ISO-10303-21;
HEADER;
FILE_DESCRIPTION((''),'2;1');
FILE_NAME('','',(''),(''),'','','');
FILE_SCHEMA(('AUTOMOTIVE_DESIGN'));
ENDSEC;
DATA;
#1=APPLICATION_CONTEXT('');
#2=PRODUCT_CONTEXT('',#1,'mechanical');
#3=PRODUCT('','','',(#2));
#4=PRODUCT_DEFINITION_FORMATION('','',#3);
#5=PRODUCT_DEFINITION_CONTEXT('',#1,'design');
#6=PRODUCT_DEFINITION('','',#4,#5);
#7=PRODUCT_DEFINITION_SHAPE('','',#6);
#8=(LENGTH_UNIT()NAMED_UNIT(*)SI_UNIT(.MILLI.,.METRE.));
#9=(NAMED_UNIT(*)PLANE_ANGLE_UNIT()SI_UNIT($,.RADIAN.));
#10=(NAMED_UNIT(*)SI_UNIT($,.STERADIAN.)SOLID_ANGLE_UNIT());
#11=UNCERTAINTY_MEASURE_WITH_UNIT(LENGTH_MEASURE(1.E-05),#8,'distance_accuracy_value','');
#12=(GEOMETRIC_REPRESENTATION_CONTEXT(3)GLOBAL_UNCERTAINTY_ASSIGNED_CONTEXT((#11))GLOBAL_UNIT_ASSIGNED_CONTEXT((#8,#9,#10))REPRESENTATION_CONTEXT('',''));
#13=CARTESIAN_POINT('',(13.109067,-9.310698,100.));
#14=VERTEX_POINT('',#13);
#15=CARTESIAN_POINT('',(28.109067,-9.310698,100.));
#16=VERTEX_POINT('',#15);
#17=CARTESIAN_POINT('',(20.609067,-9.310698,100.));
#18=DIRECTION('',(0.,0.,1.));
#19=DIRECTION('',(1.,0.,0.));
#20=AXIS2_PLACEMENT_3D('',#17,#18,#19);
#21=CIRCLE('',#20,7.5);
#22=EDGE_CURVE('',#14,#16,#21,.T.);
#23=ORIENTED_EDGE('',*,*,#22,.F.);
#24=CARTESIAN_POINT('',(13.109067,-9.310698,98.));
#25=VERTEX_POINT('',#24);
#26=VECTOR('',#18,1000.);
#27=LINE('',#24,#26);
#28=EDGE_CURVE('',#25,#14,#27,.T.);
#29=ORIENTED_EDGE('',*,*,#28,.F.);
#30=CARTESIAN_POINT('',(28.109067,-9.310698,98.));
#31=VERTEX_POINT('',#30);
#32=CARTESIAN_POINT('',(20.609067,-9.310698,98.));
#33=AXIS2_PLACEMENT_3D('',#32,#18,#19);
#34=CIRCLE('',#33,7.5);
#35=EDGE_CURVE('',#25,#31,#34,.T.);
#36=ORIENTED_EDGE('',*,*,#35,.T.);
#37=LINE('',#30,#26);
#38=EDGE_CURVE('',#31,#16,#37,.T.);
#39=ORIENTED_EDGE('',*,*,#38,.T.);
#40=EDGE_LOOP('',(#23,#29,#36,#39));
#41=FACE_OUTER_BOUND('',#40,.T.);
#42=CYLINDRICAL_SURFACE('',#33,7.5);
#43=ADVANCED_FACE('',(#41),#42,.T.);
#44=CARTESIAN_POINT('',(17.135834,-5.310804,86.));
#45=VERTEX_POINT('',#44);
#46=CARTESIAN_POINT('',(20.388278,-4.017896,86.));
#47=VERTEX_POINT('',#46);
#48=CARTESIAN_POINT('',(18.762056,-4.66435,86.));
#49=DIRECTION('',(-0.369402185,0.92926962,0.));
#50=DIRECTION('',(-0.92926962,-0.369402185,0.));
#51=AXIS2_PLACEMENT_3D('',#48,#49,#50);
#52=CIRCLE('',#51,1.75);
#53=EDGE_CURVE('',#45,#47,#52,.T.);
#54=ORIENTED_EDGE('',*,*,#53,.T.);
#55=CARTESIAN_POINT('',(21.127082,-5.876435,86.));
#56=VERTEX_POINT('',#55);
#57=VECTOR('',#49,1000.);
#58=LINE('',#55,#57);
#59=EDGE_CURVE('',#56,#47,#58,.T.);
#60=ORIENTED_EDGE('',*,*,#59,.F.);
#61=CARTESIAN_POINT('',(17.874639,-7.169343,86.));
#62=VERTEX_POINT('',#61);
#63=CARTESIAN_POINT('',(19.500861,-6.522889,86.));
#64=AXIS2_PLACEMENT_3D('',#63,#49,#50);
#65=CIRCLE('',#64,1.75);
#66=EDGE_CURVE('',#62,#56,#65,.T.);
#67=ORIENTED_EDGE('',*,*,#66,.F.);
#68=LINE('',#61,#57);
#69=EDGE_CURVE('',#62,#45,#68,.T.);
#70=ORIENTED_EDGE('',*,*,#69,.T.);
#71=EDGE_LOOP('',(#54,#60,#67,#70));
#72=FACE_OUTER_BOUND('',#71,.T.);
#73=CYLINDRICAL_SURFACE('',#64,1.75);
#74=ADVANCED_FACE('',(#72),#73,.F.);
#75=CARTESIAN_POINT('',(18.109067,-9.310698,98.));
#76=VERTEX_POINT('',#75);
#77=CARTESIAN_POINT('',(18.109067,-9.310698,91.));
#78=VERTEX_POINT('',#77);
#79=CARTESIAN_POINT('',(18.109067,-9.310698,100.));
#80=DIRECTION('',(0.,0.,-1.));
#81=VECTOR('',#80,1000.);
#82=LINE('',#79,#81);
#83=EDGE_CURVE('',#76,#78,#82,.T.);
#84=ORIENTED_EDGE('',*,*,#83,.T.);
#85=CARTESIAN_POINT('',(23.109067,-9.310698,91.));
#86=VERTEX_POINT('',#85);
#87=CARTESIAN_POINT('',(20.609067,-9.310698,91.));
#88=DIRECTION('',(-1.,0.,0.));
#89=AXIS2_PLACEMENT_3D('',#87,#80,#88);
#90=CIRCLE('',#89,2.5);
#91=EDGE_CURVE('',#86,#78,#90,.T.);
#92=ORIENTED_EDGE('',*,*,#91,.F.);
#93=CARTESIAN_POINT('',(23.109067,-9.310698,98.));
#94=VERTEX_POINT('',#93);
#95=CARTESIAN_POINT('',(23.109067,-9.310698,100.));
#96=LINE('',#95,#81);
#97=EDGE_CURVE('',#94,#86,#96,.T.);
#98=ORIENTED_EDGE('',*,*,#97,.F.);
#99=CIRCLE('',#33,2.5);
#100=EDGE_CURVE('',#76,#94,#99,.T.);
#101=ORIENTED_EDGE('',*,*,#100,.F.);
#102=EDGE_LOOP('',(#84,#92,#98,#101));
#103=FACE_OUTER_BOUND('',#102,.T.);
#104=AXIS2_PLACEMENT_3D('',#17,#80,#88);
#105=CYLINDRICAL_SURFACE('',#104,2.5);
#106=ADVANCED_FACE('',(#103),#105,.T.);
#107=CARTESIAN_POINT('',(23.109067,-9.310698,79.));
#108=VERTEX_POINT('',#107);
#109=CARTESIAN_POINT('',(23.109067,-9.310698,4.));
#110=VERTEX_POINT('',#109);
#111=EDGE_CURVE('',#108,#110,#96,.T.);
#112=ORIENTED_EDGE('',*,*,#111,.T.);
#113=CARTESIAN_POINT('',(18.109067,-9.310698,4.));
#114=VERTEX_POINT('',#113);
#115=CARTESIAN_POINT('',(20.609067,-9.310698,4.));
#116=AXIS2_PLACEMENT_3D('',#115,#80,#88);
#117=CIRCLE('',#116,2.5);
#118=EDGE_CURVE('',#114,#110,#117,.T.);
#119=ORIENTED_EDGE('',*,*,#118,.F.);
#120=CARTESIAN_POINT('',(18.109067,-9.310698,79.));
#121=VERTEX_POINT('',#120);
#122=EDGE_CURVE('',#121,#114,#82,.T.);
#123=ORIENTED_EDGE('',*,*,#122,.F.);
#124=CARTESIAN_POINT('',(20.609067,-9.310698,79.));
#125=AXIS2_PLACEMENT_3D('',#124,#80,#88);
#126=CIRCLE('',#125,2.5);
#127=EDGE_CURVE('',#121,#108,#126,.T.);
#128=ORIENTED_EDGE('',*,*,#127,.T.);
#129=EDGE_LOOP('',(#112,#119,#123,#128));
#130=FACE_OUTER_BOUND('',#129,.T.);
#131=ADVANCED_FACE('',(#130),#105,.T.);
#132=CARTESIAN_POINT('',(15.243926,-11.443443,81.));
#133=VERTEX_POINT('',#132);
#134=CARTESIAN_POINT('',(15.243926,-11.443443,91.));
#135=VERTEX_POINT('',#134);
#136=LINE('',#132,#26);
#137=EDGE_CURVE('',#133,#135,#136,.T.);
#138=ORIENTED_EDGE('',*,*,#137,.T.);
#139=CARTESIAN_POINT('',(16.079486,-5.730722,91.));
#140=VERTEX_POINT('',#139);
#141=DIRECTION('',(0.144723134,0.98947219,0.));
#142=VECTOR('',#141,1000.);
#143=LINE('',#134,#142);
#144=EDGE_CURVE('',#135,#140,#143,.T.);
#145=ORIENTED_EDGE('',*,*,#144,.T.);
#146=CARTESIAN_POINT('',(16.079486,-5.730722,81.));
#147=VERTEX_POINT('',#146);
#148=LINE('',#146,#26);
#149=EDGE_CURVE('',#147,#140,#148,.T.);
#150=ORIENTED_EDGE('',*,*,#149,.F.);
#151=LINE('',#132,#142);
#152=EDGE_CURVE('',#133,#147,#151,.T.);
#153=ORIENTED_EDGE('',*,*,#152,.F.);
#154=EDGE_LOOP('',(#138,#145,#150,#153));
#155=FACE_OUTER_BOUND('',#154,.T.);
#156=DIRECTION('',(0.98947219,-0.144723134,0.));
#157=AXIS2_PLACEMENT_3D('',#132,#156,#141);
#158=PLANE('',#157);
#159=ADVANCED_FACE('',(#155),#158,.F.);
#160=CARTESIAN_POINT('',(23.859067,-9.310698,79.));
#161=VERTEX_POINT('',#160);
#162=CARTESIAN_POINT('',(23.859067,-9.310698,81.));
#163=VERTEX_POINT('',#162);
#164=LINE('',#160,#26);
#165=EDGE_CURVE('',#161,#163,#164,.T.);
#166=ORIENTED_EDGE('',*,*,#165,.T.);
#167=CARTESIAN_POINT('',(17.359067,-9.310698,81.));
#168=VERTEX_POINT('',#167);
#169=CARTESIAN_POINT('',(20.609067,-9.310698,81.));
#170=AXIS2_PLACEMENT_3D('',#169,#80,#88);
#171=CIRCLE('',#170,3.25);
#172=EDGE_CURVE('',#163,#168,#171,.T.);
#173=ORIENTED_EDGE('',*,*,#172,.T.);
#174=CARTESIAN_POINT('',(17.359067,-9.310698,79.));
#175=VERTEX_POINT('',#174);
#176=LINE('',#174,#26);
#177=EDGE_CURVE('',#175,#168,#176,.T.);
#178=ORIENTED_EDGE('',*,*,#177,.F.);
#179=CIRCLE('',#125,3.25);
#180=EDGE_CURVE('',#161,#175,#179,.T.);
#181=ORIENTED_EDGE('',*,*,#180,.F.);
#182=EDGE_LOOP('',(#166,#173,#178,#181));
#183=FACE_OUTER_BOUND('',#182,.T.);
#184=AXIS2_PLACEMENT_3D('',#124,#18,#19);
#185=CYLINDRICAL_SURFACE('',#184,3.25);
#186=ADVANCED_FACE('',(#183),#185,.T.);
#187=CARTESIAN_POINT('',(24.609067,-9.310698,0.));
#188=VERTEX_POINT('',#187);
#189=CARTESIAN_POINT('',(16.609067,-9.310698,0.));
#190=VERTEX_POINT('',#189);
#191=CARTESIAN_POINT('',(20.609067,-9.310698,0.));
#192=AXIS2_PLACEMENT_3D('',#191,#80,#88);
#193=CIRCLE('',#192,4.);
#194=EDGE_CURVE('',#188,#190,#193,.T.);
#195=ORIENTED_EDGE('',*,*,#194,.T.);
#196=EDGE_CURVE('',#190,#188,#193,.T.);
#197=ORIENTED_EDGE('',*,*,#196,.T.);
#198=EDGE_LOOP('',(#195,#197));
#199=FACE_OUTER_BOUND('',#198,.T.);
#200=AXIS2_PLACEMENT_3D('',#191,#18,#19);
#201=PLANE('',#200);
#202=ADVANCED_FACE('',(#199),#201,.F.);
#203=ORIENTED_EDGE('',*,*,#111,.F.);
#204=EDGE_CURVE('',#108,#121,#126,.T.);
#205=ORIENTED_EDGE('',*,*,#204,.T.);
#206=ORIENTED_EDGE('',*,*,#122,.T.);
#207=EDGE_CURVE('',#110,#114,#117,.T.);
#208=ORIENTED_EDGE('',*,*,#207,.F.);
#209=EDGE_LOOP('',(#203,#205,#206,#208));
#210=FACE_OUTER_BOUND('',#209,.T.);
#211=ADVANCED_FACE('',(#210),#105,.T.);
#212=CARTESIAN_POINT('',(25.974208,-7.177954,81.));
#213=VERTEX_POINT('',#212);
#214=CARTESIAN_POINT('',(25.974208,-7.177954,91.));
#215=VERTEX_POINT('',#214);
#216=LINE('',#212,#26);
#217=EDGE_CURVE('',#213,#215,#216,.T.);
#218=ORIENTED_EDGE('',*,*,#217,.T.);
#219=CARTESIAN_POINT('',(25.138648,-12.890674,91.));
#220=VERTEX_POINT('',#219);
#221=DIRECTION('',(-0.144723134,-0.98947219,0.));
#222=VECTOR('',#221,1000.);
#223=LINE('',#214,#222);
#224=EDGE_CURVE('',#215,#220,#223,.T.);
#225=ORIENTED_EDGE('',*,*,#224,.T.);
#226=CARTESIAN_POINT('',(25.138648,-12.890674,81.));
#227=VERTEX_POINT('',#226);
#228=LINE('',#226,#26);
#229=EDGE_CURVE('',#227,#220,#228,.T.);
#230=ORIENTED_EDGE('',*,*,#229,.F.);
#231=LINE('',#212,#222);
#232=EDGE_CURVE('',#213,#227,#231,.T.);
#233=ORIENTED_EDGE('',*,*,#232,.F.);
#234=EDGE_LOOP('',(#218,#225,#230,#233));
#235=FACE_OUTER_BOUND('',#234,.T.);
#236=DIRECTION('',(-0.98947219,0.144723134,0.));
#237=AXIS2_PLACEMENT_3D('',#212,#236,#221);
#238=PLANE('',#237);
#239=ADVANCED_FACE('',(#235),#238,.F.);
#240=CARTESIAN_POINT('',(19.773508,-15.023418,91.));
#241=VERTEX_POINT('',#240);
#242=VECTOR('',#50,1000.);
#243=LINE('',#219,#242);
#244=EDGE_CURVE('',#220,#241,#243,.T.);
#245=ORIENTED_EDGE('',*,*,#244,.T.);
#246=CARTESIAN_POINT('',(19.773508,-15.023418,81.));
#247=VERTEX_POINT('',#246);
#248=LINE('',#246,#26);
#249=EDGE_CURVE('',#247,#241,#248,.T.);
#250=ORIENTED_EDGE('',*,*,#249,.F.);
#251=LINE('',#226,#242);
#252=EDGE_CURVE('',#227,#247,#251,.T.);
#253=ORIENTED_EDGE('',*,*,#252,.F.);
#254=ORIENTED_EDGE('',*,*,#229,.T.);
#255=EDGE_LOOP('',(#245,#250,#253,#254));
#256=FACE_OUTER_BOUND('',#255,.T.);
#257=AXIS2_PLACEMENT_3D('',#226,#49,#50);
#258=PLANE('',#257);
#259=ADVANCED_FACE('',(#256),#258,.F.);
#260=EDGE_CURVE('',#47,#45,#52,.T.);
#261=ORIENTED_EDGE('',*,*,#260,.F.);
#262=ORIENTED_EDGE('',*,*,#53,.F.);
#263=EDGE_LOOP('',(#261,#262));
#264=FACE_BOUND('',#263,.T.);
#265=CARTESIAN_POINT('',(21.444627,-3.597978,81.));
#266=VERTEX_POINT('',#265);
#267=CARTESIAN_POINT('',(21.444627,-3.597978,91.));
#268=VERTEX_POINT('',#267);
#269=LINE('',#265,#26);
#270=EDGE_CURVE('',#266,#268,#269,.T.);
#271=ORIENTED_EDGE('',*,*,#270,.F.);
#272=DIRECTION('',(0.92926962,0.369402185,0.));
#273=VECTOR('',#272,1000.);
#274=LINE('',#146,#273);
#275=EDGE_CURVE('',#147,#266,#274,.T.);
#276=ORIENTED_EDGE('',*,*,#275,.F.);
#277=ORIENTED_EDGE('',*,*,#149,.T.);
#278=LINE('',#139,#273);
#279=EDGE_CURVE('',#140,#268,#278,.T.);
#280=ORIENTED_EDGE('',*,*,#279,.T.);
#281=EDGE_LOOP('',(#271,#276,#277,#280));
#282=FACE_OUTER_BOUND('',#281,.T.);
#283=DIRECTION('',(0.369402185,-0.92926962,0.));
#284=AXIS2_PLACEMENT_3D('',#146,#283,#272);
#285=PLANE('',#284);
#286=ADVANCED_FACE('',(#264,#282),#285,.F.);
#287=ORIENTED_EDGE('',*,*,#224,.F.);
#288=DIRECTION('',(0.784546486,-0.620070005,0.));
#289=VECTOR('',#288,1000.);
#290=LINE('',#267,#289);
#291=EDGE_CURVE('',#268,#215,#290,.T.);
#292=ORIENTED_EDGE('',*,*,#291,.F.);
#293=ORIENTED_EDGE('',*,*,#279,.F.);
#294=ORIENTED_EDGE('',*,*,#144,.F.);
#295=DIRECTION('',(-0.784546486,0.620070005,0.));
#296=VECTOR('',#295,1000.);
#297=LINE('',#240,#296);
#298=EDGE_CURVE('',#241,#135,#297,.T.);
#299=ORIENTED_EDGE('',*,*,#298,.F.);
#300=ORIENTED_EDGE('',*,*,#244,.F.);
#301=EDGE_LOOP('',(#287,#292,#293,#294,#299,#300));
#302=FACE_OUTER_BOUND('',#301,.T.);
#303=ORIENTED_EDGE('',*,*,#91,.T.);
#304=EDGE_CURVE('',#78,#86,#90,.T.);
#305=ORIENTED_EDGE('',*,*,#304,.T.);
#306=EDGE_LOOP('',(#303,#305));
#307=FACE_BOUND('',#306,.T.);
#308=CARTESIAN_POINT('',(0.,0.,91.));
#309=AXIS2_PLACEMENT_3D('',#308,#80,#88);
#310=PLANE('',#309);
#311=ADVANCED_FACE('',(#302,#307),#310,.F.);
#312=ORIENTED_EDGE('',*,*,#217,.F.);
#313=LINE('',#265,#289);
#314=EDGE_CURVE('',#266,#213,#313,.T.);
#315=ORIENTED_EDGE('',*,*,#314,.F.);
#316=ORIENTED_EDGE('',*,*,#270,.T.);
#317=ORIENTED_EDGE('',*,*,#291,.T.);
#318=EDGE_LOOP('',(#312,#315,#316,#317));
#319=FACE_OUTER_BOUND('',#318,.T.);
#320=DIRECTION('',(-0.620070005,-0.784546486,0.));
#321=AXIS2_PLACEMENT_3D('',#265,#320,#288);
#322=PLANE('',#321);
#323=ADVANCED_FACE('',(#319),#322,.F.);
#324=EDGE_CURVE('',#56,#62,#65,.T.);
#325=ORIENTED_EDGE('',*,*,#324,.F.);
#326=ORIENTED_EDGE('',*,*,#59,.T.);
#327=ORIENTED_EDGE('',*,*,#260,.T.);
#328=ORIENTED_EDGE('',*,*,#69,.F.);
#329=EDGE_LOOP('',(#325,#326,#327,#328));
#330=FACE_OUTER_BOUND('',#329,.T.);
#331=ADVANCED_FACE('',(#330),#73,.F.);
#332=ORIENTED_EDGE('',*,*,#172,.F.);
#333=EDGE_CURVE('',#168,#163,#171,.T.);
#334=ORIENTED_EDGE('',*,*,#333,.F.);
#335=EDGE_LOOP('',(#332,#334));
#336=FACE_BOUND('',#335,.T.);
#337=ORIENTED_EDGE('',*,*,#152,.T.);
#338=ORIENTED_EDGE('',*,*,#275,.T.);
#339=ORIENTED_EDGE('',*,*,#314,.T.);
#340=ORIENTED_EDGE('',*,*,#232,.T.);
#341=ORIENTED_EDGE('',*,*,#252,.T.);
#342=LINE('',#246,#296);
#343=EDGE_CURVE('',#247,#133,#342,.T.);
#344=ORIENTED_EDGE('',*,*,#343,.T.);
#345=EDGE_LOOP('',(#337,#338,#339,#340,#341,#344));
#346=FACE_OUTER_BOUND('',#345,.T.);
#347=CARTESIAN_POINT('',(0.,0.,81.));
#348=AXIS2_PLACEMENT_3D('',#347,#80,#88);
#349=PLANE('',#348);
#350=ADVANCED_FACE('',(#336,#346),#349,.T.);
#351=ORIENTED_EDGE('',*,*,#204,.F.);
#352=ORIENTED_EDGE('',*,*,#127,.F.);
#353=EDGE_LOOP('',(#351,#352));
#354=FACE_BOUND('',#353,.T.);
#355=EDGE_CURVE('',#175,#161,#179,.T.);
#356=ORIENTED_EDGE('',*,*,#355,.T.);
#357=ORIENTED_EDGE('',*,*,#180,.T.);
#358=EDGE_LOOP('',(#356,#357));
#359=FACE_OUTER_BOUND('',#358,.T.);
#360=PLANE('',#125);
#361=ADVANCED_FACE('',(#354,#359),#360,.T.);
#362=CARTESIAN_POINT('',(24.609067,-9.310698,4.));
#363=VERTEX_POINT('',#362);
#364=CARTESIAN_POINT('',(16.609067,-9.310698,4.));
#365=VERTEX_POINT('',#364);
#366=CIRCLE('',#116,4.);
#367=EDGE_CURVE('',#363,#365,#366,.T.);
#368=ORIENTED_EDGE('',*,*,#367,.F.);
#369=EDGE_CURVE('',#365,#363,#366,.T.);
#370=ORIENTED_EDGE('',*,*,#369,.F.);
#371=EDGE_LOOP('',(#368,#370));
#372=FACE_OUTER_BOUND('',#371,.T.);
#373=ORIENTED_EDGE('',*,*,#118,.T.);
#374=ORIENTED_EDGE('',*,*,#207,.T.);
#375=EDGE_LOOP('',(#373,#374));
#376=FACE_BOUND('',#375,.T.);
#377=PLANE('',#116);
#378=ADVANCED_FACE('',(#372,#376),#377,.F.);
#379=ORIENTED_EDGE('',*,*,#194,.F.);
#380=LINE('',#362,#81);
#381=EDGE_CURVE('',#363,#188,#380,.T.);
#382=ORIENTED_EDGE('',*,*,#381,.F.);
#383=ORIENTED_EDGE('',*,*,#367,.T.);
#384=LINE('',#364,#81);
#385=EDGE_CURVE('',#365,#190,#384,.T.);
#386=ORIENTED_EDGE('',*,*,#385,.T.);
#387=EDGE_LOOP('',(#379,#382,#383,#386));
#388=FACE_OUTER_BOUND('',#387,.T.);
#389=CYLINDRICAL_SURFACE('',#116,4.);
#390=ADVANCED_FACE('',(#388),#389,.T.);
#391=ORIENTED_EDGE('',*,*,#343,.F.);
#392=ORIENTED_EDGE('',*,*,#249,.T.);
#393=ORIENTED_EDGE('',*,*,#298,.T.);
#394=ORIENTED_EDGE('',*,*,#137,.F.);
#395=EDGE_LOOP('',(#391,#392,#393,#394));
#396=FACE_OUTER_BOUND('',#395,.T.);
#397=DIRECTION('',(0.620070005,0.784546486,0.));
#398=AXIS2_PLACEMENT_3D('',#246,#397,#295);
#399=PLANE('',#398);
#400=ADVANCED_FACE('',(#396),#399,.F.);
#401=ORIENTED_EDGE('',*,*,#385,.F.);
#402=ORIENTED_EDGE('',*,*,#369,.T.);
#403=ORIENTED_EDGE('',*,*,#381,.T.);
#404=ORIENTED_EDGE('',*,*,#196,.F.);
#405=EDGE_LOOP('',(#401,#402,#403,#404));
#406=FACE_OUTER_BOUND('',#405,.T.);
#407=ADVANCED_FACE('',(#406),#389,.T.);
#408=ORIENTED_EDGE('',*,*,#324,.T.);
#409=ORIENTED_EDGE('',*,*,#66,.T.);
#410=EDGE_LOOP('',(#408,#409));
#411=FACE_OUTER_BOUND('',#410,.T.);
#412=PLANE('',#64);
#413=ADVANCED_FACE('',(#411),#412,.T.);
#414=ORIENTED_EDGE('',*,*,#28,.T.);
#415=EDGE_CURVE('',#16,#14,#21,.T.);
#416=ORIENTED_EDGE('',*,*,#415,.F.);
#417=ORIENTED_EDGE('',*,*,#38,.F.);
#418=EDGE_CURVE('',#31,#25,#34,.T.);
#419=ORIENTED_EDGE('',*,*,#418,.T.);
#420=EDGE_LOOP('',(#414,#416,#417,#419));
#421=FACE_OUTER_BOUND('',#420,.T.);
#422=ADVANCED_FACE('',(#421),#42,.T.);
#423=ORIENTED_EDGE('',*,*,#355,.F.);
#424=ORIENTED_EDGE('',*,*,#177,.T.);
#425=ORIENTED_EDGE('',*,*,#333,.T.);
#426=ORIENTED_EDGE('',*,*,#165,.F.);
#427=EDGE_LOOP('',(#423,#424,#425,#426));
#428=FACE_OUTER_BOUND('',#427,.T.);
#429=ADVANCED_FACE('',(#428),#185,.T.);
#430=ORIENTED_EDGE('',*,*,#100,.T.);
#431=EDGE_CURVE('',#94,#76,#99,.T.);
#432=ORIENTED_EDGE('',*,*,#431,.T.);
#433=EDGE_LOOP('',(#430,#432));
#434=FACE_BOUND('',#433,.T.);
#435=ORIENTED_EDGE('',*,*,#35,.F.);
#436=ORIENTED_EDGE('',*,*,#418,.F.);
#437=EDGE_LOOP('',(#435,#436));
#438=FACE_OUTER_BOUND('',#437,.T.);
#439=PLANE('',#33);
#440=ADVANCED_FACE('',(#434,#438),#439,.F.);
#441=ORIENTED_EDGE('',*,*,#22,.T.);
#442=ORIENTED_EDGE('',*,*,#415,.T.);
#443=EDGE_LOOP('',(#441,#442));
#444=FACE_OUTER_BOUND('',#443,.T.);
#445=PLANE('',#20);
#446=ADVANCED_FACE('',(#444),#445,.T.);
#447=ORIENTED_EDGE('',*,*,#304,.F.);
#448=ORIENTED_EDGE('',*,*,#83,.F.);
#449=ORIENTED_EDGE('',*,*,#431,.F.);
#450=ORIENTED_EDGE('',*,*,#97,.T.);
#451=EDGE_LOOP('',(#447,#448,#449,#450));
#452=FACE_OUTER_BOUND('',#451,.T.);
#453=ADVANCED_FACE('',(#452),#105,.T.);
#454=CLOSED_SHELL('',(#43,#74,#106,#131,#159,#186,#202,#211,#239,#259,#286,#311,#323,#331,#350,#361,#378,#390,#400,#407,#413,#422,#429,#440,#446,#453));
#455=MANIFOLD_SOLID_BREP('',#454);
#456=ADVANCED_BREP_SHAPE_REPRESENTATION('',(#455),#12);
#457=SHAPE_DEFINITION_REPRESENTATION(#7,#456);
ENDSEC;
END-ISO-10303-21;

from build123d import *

# Parameters (mm, degrees)
SKETCH2_R           = 2.5
BOSS_EXTRUDE1_DEPTH = 100
SKETCH3_R           = 4
BOSS_EXTRUDE2_DEPTH = 4
SKETCH4_R           = 7.5
BOSS_EXTRUDE3_DEPTH = 2
BOSS_EXTRUDE4_DEPTH = 10
SKETCH6_R           = 3.25
BOSS_EXTRUDE5_DEPTH = 2
SKETCH7_R           = 1.75
CUT_EXTRUDE1_DEPTH  = 2


with BuildPart() as part:
    # Sketch2 → Boss-Extrude1 (new body)
    with BuildSketch(Plane.XY):
        with Locations((20.609067119, -9.310698144)):
            Circle(SKETCH2_R)
    extrude(amount=BOSS_EXTRUDE1_DEPTH)

    # Sketch3 → Boss-Extrude2 (add)
    with BuildSketch(Plane(origin=(0, 0, 0), x_dir=(-1, 0, 0), z_dir=(0, 0, -1))):
        with Locations((-20.609067119, -9.310698144)):
            Circle(SKETCH3_R)
    extrude(amount=-BOSS_EXTRUDE2_DEPTH)

    # Sketch4 → Boss-Extrude3 (add)
    with BuildSketch(Plane.XY.offset(100)):
        with Locations((20.609067119, -9.310698144)):
            Circle(SKETCH4_R)
    extrude(amount=-BOSS_EXTRUDE3_DEPTH)

    # Sketch5 → Boss-Extrude4 (add)
    with BuildSketch(Plane(origin=(0, 0, 91), x_dir=(-1, 0, 0), z_dir=(0, 0, -1))):
        Polygon((-16.079485871, -5.730722299), (-21.444626522, -3.597977792), (-25.97420777, -7.177953637), (-25.138648367, -12.890673989), (-19.773507717, -15.023418496), (-15.243926469, -11.443442651), align=None)
    extrude(amount=BOSS_EXTRUDE4_DEPTH)

    # Sketch6 → Boss-Extrude5 (add)
    with BuildSketch(Plane(origin=(0, 0, 81), x_dir=(-1, 0, 0), z_dir=(0, 0, -1))):
        with Locations((-20.609067119, -9.310698144)):
            Circle(SKETCH6_R)
    extrude(amount=BOSS_EXTRUDE5_DEPTH)

    # Sketch7 → Cut-Extrude1 (cut)
    with BuildSketch(Plane(origin=(4.161383334, -10.468392636, 0), x_dir=(0.9292696196810543, 0.3694021845331033, 0), z_dir=(-0.3694021845331033, 0.9292696196810543, 0))):
        with Locations(Location((15.71198773, -86, 0), (0, 0, 180))):
            Circle(SKETCH7_R)
    extrude(amount=-CUT_EXTRUDE1_DEPTH, mode=Mode.SUBTRACT)


solid = part.part
